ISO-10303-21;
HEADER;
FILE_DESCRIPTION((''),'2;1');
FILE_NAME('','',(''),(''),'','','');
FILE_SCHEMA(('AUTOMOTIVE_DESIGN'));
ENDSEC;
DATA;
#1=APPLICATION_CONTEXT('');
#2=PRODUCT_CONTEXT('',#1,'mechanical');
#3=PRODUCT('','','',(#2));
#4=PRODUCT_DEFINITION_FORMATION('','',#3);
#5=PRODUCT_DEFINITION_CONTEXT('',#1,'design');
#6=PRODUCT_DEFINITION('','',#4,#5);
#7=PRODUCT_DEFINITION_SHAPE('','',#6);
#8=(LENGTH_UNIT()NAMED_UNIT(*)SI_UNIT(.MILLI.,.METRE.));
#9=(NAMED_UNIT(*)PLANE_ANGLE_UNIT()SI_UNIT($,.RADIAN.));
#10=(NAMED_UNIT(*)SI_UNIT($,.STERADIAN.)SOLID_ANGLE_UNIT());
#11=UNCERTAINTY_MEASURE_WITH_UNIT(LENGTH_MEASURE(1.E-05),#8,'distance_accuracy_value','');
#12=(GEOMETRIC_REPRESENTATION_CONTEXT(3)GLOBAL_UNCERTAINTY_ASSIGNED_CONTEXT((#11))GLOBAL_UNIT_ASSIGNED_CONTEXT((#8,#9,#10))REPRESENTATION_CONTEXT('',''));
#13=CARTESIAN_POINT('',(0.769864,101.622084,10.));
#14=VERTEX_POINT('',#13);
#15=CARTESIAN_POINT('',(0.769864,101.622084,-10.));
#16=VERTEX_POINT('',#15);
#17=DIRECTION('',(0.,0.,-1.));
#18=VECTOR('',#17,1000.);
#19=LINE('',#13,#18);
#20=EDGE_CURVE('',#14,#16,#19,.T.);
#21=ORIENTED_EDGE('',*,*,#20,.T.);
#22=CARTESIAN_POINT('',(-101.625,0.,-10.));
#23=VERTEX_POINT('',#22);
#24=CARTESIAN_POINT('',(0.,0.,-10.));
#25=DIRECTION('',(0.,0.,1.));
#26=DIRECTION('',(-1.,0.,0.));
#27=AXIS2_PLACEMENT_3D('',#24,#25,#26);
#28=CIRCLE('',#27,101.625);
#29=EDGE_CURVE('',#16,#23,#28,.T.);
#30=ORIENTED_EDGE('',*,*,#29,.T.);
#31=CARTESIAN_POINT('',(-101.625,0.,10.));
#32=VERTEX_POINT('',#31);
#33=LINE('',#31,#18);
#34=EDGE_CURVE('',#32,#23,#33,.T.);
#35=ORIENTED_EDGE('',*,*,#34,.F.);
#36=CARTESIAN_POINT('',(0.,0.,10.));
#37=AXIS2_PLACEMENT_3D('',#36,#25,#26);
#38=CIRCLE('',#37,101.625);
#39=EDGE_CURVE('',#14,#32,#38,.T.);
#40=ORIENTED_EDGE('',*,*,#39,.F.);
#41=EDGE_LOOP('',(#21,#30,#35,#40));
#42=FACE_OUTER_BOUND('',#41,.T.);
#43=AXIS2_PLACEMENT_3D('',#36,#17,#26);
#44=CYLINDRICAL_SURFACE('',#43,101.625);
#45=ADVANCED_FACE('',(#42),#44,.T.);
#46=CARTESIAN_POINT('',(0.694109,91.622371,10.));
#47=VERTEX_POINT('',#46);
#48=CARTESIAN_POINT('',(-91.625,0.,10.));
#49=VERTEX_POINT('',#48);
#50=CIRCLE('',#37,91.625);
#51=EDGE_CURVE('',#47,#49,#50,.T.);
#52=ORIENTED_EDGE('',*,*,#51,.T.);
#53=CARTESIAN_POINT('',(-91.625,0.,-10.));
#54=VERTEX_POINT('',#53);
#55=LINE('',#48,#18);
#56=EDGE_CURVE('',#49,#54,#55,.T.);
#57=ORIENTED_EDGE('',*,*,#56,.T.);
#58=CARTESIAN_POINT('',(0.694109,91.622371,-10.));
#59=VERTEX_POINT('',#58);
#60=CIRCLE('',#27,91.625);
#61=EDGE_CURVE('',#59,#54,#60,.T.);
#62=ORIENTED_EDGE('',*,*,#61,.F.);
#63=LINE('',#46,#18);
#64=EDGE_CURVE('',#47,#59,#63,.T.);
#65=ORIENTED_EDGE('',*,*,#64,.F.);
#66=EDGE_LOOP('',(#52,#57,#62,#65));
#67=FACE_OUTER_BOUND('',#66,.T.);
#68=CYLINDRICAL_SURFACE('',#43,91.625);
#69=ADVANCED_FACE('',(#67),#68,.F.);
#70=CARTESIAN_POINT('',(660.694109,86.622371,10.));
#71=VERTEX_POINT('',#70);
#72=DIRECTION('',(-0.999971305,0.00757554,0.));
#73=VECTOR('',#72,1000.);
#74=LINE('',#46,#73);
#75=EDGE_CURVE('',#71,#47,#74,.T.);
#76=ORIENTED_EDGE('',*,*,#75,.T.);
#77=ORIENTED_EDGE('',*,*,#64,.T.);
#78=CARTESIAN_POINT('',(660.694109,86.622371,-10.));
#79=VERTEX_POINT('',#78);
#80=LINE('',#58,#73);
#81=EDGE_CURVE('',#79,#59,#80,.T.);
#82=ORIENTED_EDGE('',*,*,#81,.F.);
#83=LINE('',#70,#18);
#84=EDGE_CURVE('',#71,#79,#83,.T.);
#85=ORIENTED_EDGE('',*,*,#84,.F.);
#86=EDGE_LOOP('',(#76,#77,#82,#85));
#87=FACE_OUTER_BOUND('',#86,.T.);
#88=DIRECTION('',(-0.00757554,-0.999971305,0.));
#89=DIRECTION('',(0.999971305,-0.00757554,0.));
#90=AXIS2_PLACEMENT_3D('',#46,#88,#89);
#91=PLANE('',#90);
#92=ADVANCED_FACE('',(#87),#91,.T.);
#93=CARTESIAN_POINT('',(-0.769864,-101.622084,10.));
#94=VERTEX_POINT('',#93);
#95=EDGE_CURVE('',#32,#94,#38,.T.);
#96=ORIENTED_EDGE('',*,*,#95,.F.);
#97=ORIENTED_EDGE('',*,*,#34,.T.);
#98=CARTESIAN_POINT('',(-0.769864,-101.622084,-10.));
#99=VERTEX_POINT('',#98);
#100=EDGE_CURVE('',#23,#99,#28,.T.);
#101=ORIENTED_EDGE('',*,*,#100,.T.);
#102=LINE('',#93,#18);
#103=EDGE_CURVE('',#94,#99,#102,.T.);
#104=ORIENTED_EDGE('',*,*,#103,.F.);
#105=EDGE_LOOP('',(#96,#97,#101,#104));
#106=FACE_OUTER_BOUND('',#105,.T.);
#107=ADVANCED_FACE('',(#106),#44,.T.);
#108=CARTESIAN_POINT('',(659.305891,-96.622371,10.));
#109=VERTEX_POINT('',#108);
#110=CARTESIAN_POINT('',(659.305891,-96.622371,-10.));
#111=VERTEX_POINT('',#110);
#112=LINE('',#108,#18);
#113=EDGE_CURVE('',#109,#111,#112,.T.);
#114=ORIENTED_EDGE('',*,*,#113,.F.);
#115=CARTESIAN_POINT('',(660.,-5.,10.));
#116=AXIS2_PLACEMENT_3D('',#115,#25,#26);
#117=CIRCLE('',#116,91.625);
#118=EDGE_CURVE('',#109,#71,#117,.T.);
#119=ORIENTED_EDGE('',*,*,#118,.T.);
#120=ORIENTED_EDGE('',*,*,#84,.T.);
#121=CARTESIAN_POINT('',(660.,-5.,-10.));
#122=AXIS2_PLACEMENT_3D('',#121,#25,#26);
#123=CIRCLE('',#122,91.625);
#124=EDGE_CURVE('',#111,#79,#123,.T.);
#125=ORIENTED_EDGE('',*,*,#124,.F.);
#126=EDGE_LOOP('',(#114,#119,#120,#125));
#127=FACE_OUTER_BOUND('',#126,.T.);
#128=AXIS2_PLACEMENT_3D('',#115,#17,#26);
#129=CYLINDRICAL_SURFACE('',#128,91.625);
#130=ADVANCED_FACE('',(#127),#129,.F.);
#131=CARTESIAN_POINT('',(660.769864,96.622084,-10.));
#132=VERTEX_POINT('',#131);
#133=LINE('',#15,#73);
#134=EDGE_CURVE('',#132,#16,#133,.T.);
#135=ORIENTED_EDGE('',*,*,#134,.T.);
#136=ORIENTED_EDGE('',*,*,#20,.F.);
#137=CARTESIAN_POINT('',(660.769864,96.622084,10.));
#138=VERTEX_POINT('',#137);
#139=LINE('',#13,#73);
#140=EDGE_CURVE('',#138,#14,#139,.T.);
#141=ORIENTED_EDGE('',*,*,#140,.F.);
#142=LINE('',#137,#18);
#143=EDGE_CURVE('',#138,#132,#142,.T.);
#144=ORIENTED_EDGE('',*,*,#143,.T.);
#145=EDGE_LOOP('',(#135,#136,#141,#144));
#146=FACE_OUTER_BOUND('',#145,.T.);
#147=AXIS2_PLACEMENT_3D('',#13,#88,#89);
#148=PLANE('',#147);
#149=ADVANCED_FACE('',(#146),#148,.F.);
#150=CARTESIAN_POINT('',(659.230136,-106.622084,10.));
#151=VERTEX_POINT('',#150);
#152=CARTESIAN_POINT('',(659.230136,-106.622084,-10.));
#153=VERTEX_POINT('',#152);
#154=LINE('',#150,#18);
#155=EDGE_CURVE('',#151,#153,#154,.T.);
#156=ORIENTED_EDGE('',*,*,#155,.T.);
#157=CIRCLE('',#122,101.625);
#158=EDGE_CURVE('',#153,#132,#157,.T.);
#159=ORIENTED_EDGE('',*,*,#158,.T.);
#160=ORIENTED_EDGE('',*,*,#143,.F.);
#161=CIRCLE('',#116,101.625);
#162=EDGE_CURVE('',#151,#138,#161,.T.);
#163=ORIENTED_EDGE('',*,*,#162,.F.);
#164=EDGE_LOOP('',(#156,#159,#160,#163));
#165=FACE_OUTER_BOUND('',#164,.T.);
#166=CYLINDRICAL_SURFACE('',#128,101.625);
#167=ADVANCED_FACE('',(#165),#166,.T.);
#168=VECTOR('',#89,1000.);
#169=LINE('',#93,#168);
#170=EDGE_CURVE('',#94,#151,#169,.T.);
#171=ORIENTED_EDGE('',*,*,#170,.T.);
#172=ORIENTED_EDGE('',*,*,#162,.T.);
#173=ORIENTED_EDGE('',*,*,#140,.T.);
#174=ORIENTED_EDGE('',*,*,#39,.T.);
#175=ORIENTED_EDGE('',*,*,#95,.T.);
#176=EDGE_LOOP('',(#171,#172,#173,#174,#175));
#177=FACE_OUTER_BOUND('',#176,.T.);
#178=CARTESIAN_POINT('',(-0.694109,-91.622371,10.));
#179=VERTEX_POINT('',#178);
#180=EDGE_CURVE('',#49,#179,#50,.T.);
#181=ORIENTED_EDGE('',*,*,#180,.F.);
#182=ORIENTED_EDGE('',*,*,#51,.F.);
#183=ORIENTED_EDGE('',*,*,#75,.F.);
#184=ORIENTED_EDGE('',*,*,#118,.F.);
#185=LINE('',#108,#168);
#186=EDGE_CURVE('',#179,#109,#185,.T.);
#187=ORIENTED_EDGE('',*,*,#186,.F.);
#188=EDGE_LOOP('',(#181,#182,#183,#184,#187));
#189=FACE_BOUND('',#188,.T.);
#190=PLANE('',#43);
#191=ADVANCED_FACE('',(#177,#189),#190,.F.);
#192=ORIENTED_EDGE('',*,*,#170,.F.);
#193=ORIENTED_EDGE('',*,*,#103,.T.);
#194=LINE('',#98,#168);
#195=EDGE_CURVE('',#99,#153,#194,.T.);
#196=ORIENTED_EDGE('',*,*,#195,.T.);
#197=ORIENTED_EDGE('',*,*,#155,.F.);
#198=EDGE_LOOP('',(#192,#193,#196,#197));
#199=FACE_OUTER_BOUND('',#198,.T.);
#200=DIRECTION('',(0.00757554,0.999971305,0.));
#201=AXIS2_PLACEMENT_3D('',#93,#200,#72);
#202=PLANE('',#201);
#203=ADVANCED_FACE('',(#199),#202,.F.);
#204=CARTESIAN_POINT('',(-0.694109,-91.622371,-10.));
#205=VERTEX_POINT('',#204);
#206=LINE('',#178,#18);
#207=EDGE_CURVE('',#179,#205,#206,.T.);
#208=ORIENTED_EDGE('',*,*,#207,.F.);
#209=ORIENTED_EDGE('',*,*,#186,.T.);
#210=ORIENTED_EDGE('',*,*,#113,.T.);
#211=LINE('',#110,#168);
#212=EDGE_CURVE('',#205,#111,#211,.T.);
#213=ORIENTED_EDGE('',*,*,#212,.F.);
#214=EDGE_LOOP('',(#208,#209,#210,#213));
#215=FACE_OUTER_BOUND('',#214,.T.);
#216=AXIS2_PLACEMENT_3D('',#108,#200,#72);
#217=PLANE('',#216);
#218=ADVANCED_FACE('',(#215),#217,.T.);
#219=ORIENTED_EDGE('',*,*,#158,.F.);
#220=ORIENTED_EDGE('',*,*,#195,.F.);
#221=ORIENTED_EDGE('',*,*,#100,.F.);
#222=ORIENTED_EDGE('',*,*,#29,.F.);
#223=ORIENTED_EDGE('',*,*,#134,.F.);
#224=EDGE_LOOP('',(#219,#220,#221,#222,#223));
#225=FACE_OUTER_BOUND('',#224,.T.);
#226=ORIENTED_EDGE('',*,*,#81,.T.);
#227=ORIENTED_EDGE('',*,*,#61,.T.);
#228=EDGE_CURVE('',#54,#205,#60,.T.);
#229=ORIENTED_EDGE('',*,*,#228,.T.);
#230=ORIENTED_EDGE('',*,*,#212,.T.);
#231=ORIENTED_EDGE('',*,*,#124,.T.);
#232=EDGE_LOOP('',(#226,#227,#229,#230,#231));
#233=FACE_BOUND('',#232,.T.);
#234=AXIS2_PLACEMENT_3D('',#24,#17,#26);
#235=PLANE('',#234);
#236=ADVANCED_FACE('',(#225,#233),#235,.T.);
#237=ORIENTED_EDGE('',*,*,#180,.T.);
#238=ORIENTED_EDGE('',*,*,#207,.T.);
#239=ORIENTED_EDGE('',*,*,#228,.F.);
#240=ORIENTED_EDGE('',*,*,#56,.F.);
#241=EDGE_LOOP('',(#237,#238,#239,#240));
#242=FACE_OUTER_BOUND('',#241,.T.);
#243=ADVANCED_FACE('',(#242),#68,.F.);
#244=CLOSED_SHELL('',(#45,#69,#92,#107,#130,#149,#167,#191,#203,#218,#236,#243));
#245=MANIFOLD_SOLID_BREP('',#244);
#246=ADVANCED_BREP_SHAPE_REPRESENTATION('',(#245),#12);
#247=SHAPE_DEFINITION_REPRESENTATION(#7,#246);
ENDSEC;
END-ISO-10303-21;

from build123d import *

# Parameters (mm, degrees)
EXTRUDE_1_DEPTH = 10


with BuildPart() as part:
    # 草图2 → 拉伸-薄壁1 (new, symmetric)
    with BuildSketch(Plane.XY):
        with BuildLine():
            Line((659.230135728, -106.622083889), (-0.769864272, -101.622083889))
            ThreePointArc((-0.769864272, -101.622083889), (-101.622083889, 0.769864272), (0.769864272, 101.622083889))
            Line((0.769864272, 101.622083889), (660.769864272, 96.622083889))
            ThreePointArc((660.769864272, 96.622083889), (761.622083889, -5.769864272), (659.230135728, -106.622083889))
        make_face()
        with BuildLine():
            Line((659.30589113, -96.622370837), (-0.69410887, -91.622370837))
            ThreePointArc((-0.69410887, -91.622370837), (-91.622370837, 0.69410887), (0.69410887, 91.622370837))
            Line((0.69410887, 91.622370837), (660.69410887, 86.622370837))
            ThreePointArc((660.69410887, 86.622370837), (751.622370837, -5.69410887), (659.30589113, -96.622370837))
        make_face(mode=Mode.SUBTRACT)
    extrude(amount=EXTRUDE_1_DEPTH, both=True)


solid = part.part
